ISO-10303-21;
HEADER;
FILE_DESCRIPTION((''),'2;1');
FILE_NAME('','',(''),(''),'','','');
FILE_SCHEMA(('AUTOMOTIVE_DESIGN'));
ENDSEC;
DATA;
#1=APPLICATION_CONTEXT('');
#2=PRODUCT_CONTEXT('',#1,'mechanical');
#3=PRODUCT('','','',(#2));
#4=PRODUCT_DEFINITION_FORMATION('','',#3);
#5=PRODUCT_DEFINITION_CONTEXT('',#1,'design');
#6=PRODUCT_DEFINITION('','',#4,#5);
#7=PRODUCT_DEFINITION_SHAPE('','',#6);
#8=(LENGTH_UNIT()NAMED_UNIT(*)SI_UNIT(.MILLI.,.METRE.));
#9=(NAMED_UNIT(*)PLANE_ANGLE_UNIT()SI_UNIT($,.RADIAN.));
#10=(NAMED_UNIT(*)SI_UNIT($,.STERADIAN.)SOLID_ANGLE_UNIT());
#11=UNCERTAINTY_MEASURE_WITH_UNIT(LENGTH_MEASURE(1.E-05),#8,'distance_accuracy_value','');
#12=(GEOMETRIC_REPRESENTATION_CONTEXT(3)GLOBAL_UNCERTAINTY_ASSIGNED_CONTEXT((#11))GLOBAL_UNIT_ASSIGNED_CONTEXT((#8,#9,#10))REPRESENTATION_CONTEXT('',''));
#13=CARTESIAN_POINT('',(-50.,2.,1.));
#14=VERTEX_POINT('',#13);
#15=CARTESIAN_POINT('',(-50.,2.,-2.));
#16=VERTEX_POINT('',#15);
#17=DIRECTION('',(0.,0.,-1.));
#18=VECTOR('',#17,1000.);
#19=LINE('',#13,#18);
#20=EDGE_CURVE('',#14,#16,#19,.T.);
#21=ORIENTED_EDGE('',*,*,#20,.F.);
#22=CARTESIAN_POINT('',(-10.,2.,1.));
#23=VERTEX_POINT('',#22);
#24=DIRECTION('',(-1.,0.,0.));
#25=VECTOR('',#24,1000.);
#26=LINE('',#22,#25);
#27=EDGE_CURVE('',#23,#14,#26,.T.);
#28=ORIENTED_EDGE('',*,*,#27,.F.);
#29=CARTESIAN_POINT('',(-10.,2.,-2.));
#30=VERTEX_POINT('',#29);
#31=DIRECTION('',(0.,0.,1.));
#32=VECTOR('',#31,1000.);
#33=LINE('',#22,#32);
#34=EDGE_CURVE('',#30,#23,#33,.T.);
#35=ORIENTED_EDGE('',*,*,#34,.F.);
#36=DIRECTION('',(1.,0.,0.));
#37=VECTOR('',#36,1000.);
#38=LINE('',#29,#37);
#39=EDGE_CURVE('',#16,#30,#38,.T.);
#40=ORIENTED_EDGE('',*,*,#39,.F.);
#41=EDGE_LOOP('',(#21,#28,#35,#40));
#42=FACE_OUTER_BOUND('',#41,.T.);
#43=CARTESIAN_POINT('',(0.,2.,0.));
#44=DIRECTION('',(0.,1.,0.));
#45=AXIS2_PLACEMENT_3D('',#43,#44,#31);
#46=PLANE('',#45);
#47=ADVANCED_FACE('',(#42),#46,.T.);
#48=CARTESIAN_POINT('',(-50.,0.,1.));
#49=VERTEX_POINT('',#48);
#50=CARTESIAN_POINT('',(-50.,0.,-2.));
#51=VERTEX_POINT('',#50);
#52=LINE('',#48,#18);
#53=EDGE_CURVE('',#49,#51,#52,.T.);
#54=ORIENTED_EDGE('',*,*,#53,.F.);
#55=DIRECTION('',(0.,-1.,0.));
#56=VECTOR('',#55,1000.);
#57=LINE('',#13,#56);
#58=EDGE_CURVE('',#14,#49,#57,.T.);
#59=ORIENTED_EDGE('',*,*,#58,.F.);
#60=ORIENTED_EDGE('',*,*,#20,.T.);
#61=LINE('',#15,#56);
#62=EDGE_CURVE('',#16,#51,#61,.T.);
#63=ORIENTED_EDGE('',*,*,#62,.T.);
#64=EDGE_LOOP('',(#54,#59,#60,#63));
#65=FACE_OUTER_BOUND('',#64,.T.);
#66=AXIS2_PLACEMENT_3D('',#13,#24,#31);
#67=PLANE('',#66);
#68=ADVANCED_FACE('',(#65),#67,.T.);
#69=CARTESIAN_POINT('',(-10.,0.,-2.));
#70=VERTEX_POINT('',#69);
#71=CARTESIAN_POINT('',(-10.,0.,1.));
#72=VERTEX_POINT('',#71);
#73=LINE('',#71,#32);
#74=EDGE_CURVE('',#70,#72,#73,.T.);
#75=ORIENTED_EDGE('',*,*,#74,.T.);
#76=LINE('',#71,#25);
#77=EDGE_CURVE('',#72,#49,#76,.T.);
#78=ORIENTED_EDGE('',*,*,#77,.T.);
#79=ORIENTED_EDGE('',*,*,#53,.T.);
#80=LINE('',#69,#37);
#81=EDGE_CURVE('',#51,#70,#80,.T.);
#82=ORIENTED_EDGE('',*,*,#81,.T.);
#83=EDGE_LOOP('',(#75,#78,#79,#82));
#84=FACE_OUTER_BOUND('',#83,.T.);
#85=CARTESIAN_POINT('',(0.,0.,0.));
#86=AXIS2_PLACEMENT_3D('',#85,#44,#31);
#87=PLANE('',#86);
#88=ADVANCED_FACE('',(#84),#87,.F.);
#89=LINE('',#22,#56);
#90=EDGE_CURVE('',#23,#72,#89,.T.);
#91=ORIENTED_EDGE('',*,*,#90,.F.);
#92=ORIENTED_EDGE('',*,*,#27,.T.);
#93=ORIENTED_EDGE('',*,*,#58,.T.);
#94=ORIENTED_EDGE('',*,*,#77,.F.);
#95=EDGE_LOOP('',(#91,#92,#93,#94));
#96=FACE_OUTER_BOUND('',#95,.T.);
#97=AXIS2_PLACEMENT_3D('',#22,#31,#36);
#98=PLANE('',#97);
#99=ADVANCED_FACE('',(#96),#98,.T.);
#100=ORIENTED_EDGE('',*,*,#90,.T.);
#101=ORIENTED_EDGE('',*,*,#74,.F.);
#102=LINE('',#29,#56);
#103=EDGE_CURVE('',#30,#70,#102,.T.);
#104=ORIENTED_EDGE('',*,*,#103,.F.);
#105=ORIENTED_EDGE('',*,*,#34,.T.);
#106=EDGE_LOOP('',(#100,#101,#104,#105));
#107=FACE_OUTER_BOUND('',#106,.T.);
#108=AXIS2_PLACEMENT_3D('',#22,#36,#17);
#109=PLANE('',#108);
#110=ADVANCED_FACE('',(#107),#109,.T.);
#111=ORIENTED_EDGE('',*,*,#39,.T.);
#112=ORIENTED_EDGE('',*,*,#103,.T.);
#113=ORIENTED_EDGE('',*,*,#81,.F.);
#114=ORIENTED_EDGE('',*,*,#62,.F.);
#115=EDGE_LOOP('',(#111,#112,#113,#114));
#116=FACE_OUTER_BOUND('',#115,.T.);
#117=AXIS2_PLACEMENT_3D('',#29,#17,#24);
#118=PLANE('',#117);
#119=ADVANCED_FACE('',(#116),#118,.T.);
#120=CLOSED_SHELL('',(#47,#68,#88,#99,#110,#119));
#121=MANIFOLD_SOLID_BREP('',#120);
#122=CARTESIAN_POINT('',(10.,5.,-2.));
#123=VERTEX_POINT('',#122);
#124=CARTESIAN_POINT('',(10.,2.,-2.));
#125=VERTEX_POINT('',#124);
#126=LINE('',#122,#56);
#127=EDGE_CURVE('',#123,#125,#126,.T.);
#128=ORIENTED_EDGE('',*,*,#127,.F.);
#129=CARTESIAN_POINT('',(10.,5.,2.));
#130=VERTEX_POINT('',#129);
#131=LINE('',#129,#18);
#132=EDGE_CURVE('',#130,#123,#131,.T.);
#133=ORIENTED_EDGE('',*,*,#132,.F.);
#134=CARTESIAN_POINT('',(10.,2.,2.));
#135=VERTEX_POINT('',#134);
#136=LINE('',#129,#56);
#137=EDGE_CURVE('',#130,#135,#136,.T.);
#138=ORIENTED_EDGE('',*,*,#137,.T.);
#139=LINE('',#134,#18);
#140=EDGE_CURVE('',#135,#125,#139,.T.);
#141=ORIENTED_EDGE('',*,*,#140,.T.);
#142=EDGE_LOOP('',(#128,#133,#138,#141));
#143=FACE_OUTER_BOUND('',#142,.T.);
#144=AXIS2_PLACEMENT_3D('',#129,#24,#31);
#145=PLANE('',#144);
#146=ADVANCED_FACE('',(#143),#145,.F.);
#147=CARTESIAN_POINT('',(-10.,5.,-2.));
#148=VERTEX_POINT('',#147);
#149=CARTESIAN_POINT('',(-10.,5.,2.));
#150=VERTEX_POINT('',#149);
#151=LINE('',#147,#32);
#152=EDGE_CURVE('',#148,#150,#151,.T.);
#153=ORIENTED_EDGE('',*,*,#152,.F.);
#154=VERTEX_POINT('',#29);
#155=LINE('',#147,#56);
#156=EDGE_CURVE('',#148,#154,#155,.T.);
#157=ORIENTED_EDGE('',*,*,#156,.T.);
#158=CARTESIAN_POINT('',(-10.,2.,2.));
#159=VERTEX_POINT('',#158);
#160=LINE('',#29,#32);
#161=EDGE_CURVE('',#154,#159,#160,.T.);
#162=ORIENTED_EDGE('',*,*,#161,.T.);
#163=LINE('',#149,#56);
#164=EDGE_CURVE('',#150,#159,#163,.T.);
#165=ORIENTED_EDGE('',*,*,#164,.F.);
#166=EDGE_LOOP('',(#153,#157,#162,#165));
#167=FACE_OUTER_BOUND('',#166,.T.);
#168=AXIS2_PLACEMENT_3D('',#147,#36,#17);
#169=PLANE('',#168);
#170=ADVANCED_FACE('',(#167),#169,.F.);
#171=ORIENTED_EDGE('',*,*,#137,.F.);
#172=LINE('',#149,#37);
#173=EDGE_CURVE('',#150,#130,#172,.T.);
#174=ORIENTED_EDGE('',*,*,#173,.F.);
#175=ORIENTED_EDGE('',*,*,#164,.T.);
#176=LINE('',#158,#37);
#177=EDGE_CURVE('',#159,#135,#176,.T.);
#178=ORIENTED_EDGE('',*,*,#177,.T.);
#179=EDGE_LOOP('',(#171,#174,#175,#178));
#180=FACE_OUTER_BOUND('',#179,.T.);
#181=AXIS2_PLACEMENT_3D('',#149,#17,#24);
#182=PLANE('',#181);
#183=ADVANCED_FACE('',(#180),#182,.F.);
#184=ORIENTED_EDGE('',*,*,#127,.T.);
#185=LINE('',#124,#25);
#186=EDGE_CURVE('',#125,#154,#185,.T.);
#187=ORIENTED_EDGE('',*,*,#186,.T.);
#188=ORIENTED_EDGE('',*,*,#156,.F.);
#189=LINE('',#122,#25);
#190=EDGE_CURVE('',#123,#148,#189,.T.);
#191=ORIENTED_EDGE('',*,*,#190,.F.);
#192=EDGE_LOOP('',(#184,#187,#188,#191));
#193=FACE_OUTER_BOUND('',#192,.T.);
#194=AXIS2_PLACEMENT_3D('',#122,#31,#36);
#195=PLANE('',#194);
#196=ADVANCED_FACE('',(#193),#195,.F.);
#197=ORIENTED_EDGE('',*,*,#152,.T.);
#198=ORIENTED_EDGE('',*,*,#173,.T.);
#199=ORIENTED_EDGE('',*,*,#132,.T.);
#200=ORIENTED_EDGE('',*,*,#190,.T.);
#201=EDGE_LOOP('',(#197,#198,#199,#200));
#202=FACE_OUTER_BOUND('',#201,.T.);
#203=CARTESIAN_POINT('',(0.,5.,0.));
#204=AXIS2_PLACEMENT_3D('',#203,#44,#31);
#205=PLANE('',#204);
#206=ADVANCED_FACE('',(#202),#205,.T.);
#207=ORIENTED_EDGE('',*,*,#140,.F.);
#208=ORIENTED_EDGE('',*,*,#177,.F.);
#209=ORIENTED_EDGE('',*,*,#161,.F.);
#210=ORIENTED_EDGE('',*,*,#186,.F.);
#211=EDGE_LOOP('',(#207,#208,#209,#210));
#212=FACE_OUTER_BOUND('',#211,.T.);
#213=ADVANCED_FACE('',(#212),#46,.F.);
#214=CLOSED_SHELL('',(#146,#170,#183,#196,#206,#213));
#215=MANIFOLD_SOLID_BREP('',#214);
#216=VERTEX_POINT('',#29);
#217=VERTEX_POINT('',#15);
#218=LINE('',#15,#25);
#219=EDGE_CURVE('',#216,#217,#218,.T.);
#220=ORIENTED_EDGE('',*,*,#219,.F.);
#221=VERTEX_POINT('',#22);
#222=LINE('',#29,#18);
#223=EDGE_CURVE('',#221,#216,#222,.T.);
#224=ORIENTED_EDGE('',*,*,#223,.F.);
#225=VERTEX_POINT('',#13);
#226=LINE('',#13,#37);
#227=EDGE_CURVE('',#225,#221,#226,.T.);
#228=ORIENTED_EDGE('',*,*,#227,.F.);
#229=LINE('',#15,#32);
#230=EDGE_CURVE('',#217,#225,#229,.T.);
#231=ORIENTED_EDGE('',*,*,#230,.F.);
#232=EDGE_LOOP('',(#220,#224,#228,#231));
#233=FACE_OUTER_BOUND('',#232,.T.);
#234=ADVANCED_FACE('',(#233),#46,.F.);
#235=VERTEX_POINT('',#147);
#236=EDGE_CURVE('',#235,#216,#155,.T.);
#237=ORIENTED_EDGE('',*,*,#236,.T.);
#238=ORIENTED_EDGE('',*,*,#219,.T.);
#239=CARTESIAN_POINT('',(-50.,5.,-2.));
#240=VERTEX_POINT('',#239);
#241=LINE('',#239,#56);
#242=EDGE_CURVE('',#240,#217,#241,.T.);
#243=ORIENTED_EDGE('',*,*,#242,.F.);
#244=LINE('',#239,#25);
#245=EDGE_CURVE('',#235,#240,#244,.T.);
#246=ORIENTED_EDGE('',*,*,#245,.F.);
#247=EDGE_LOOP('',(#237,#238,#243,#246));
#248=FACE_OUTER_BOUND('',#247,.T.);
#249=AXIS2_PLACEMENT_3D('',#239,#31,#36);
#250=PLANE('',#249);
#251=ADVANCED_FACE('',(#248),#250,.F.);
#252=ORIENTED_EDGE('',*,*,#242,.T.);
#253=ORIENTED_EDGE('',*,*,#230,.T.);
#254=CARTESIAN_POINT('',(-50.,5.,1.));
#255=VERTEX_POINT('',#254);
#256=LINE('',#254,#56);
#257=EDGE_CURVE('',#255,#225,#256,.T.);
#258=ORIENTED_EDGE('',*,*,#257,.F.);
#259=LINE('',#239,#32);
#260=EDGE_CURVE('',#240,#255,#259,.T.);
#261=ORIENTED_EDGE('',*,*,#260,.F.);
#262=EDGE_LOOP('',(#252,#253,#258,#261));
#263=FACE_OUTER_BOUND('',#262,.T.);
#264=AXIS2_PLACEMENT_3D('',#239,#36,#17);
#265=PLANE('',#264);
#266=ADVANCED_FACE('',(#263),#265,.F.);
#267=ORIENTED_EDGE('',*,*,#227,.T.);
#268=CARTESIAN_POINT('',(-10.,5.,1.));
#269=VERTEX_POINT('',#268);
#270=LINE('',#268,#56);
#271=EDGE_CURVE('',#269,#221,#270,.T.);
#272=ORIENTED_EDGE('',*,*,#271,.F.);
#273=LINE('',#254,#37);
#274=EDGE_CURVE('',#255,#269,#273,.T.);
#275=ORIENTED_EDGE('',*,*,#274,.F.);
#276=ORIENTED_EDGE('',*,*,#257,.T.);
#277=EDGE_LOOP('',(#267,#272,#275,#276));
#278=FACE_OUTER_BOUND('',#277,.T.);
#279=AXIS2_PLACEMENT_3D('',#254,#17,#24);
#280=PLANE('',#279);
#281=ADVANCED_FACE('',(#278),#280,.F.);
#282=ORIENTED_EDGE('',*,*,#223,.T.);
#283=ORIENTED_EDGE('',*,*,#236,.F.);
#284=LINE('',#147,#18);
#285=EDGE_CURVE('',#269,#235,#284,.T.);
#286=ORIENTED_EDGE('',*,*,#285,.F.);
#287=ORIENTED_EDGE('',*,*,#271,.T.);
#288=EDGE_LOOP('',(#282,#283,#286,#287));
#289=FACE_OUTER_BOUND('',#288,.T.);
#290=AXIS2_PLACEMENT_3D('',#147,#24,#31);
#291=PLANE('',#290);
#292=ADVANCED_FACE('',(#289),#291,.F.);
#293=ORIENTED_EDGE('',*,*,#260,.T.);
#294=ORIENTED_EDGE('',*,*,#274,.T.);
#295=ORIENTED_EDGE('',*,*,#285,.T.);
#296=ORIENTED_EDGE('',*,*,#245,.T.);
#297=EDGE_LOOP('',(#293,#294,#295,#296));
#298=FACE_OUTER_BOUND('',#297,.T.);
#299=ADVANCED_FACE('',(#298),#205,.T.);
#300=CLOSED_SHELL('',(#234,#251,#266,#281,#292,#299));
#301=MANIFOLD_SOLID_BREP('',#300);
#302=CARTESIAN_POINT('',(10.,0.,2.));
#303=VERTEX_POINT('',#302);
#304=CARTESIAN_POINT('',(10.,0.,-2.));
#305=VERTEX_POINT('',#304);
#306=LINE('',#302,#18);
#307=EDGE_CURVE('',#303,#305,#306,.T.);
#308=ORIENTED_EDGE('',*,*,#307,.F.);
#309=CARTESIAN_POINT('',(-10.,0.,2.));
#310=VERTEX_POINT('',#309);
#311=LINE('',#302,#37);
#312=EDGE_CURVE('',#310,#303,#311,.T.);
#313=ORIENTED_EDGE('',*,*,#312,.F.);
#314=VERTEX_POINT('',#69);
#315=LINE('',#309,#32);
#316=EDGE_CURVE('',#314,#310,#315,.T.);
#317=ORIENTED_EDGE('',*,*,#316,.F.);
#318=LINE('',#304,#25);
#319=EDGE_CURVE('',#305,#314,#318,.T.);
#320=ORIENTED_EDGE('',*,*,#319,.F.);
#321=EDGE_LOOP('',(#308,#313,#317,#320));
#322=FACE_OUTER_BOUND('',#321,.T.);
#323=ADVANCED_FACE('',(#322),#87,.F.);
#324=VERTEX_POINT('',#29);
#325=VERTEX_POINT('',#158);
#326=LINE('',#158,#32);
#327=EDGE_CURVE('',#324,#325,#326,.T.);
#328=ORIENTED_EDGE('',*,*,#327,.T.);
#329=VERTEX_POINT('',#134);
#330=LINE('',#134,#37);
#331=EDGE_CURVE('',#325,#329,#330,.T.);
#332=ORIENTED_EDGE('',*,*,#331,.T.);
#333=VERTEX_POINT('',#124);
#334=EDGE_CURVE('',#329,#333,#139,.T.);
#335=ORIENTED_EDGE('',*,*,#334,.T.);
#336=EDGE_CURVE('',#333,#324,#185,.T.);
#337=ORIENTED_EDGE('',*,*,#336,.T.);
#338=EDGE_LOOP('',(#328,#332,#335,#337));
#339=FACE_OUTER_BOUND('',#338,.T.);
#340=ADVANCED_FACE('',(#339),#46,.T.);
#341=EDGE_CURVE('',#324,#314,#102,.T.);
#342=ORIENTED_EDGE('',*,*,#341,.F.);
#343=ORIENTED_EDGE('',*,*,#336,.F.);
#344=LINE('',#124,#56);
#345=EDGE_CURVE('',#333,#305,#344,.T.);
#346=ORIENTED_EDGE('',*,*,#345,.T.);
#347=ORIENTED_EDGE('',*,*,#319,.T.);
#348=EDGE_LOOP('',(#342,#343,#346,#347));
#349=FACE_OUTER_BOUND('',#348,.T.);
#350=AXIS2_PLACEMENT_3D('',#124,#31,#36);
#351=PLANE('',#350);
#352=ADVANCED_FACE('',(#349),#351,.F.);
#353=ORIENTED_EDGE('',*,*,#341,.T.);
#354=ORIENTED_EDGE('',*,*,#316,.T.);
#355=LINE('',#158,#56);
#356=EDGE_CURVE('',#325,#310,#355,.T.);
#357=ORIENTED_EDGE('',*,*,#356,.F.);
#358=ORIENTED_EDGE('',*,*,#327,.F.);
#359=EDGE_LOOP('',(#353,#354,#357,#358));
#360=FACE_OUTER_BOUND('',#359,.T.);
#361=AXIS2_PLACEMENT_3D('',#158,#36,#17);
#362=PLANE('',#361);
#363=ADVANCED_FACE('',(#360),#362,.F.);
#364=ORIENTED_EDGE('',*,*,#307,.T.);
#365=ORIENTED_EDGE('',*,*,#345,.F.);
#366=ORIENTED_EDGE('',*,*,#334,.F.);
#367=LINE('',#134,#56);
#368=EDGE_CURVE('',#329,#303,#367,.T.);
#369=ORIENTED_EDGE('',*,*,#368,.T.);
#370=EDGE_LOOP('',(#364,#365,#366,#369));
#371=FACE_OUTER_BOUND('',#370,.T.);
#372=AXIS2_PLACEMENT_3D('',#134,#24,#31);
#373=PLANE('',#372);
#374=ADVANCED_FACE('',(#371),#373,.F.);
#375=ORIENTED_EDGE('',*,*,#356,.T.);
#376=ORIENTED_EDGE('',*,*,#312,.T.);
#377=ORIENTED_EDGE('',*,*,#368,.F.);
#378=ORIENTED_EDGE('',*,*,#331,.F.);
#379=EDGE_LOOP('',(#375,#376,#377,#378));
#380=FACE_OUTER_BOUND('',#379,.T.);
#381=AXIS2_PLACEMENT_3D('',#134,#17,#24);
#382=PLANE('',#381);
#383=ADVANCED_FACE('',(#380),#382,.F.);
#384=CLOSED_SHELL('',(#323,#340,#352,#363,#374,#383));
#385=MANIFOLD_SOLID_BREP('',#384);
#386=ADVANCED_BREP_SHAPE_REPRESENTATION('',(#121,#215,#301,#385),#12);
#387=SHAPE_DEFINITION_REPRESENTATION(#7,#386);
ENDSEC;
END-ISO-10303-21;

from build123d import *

# Parameters (mm, degrees)
SKETCH_1_W      = 20
SKETCH_1_H      = 4
EXTRUDE_1_DEPTH = 2
SKETCH_3_W      = 20
SKETCH_3_H      = 4
EXTRUDE_2_DEPTH = 3
SKETCH_4_W      = 40
SKETCH_4_H      = 3
EXTRUDE_3_DEPTH = 2
SKETCH_5_W      = 40
SKETCH_5_H      = 3
EXTRUDE_4_DEPTH = 3


with BuildPart() as part:
    # 草图1 → 凸台-拉伸1 (new body)
    with BuildSketch(Plane(origin=(0, 0, 0), x_dir=(1, 0, 0), z_dir=(0, 1, 0))):
        Rectangle(SKETCH_1_W, SKETCH_1_H)
    extrude(amount=EXTRUDE_1_DEPTH)


with BuildPart() as body_2:
    # 草图3 → 凸台-拉伸2 (new body)
    with BuildSketch(Plane(origin=(0, 2, 0), x_dir=(1, 0, 0), z_dir=(0, 1, 0))):
        Rectangle(SKETCH_3_W, SKETCH_3_H)
    extrude(amount=EXTRUDE_2_DEPTH)


with BuildPart() as body_3:
    # 草图4 → 凸台-拉伸3 (new body)
    with BuildSketch(Plane.XZ):
        with Locations((-30, -0.5)):
            Rectangle(SKETCH_4_W, SKETCH_4_H)
    extrude(amount=-EXTRUDE_3_DEPTH)


with BuildPart() as body_4:
    # 草图5 → 凸台-拉伸4 (new body)
    with BuildSketch(Plane(origin=(0, 2, 0), x_dir=(1, 0, 0), z_dir=(0, 1, 0))):
        with Locations((-30, 0.5)):
            Rectangle(SKETCH_5_W, SKETCH_5_H)
    extrude(amount=EXTRUDE_4_DEPTH)


solid = Compound([part.part, body_2.part, body_3.part, body_4.part])
